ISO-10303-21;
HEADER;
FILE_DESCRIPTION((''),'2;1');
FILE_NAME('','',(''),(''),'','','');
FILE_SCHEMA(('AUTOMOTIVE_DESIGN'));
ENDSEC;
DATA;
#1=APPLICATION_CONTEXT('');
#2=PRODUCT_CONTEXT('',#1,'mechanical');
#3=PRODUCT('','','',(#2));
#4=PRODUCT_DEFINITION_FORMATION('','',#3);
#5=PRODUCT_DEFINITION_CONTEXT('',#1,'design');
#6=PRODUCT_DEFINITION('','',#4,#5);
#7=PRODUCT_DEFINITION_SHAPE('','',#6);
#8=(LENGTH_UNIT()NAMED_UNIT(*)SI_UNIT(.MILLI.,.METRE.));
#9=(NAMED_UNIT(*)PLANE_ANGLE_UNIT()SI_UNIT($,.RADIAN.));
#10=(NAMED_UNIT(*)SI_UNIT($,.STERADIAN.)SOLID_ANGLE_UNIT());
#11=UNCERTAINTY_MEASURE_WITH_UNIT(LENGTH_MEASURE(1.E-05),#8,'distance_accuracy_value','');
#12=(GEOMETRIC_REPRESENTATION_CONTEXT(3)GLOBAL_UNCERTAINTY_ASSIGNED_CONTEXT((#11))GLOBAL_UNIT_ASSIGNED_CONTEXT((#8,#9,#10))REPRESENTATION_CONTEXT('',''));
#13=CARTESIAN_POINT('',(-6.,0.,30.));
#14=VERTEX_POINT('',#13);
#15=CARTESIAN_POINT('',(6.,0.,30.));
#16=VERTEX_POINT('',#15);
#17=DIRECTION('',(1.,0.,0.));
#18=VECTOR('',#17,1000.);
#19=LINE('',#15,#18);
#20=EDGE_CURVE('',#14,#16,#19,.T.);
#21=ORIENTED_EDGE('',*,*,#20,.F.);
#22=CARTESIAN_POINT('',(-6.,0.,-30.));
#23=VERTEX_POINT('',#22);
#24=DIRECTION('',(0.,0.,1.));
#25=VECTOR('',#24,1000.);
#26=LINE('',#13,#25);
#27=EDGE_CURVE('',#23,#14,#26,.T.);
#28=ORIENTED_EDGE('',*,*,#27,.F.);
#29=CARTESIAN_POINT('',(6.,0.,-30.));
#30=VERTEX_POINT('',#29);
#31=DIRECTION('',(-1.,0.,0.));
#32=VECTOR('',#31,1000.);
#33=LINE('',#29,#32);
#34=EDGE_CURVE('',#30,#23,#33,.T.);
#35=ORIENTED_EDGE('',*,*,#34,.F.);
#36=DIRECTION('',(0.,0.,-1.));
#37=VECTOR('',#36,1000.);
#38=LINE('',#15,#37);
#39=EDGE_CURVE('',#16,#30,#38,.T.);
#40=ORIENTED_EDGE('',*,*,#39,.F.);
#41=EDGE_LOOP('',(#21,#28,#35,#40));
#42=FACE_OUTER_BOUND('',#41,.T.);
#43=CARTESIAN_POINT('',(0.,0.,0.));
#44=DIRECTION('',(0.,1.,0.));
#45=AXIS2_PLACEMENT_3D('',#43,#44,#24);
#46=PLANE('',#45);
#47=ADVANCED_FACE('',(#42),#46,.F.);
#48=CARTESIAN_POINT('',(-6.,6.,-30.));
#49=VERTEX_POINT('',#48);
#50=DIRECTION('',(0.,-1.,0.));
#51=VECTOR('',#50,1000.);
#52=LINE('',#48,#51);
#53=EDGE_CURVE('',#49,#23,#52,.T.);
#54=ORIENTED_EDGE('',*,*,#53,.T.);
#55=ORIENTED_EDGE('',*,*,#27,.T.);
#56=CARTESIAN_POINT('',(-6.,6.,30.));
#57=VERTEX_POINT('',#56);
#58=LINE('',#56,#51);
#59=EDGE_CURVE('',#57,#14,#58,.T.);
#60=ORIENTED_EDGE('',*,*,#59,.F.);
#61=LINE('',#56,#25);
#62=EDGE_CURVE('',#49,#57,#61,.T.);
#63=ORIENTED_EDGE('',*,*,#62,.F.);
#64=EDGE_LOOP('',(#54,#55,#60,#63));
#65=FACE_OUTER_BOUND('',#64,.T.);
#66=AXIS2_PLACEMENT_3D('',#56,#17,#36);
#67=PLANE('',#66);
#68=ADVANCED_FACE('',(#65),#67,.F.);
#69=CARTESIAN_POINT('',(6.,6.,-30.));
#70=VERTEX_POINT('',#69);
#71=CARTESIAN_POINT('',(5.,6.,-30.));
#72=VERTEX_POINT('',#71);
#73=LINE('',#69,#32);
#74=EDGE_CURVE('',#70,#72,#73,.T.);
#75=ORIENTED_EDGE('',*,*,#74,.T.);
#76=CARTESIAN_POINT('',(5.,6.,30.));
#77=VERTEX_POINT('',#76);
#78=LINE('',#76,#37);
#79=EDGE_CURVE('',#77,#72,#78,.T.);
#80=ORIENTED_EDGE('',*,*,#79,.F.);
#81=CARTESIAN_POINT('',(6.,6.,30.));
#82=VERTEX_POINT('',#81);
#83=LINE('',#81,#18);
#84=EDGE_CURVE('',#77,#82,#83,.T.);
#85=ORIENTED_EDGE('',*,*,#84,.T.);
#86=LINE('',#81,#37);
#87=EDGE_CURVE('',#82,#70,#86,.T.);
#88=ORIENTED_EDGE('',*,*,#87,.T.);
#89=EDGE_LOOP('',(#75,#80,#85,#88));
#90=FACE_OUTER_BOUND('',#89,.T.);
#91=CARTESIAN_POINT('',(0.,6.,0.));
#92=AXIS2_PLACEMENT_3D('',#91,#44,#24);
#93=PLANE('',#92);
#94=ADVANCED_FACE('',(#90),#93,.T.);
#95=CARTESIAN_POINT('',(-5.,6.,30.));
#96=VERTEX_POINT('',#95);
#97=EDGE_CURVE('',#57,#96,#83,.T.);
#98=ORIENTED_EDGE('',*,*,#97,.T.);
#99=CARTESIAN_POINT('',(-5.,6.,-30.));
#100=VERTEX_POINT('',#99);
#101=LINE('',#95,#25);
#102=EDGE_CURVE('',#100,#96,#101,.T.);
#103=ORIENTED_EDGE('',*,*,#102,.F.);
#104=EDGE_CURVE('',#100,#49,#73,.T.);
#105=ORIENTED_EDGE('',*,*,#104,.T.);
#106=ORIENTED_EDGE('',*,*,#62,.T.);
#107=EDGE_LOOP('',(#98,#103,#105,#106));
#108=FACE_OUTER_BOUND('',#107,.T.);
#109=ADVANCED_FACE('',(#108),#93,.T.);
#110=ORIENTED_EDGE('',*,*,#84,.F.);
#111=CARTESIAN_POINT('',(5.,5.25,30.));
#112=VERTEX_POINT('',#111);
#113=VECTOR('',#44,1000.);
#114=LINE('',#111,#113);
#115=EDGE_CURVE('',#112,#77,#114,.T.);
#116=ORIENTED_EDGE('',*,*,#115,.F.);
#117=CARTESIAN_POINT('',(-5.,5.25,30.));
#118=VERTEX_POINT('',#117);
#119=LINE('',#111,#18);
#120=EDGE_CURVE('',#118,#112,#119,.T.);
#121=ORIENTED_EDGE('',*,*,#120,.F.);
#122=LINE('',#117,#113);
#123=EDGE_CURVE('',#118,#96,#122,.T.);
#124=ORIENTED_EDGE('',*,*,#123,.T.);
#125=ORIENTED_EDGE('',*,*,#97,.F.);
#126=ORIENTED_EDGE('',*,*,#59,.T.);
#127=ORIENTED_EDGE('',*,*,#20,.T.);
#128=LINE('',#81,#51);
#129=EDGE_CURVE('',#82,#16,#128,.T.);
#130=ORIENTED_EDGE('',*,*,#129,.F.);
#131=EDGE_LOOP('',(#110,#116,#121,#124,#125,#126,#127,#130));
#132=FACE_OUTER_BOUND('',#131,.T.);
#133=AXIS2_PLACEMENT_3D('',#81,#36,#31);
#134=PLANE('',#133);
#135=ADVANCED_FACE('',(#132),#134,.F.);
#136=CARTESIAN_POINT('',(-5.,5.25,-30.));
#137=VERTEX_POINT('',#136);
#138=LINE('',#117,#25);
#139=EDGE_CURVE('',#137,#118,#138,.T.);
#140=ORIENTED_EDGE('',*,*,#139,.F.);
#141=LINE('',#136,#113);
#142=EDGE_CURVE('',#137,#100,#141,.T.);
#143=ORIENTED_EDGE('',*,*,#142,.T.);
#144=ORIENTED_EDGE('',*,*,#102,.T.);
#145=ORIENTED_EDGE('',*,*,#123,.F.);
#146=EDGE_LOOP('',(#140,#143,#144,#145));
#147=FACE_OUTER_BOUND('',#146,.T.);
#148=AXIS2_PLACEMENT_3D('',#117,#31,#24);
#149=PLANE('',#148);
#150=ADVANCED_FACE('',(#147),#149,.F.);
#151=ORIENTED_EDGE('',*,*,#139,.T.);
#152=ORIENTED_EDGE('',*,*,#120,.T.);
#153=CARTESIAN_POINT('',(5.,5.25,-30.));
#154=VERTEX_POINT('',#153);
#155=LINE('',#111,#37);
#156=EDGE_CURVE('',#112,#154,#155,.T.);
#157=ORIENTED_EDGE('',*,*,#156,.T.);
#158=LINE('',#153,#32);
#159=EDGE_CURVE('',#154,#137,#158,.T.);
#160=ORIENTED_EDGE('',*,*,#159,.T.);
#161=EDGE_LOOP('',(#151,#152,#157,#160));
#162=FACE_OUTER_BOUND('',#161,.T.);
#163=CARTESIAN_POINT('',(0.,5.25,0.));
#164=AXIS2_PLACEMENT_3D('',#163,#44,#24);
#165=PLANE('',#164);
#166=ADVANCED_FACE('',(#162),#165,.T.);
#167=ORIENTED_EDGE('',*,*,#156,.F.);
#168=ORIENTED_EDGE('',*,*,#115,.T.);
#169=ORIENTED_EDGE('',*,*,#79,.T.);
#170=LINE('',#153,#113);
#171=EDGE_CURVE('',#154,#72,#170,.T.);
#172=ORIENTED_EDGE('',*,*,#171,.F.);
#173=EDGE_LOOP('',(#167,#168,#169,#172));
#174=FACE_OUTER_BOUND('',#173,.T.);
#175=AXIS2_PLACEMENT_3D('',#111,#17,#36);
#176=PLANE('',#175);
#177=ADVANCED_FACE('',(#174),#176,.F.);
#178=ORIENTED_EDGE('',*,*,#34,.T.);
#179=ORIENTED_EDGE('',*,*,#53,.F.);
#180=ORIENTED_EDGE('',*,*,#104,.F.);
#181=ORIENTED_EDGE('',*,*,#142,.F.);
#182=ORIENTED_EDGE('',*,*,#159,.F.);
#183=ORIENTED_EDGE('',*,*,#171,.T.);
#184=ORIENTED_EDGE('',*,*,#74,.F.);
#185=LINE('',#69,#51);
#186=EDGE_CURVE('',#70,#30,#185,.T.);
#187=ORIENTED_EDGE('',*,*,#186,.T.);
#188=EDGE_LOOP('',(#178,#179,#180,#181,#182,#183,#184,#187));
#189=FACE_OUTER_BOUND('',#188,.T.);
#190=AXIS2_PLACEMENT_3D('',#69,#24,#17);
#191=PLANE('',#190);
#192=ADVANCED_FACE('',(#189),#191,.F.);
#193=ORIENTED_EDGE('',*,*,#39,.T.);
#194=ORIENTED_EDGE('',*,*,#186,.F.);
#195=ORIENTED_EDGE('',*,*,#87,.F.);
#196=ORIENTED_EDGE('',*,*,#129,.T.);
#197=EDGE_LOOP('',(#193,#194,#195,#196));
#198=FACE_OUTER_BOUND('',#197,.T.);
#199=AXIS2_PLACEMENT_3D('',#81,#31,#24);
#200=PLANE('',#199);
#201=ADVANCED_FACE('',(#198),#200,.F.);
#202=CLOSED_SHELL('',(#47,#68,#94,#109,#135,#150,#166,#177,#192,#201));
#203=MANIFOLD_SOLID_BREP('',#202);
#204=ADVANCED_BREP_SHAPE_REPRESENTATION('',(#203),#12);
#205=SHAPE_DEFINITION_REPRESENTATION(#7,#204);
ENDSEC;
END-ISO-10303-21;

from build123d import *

# Parameters (mm, degrees)
SKETCH_1_W          = 12
SKETCH_1_H          = 60
EXTRUDE_1_DEPTH     = 6
SKETCH_2_W          = 10
SKETCH_2_H          = 60
CUT_EXTRUDE_1_DEPTH = 0.75


with BuildPart() as part:
    # 草图1 → 凸台-拉伸1 (new body)
    with BuildSketch(Plane(origin=(0, 0, 0), x_dir=(1, 0, 0), z_dir=(0, 1, 0))):
        Rectangle(SKETCH_1_W, SKETCH_1_H)
    extrude(amount=EXTRUDE_1_DEPTH)

    # 草图2 → 切除-拉伸1 (cut)
    with BuildSketch(Plane(origin=(0, 6, 0), x_dir=(1, 0, 0), z_dir=(0, 1, 0))):
        Rectangle(SKETCH_2_W, SKETCH_2_H)
    extrude(amount=-CUT_EXTRUDE_1_DEPTH, mode=Mode.SUBTRACT)


solid = part.part
